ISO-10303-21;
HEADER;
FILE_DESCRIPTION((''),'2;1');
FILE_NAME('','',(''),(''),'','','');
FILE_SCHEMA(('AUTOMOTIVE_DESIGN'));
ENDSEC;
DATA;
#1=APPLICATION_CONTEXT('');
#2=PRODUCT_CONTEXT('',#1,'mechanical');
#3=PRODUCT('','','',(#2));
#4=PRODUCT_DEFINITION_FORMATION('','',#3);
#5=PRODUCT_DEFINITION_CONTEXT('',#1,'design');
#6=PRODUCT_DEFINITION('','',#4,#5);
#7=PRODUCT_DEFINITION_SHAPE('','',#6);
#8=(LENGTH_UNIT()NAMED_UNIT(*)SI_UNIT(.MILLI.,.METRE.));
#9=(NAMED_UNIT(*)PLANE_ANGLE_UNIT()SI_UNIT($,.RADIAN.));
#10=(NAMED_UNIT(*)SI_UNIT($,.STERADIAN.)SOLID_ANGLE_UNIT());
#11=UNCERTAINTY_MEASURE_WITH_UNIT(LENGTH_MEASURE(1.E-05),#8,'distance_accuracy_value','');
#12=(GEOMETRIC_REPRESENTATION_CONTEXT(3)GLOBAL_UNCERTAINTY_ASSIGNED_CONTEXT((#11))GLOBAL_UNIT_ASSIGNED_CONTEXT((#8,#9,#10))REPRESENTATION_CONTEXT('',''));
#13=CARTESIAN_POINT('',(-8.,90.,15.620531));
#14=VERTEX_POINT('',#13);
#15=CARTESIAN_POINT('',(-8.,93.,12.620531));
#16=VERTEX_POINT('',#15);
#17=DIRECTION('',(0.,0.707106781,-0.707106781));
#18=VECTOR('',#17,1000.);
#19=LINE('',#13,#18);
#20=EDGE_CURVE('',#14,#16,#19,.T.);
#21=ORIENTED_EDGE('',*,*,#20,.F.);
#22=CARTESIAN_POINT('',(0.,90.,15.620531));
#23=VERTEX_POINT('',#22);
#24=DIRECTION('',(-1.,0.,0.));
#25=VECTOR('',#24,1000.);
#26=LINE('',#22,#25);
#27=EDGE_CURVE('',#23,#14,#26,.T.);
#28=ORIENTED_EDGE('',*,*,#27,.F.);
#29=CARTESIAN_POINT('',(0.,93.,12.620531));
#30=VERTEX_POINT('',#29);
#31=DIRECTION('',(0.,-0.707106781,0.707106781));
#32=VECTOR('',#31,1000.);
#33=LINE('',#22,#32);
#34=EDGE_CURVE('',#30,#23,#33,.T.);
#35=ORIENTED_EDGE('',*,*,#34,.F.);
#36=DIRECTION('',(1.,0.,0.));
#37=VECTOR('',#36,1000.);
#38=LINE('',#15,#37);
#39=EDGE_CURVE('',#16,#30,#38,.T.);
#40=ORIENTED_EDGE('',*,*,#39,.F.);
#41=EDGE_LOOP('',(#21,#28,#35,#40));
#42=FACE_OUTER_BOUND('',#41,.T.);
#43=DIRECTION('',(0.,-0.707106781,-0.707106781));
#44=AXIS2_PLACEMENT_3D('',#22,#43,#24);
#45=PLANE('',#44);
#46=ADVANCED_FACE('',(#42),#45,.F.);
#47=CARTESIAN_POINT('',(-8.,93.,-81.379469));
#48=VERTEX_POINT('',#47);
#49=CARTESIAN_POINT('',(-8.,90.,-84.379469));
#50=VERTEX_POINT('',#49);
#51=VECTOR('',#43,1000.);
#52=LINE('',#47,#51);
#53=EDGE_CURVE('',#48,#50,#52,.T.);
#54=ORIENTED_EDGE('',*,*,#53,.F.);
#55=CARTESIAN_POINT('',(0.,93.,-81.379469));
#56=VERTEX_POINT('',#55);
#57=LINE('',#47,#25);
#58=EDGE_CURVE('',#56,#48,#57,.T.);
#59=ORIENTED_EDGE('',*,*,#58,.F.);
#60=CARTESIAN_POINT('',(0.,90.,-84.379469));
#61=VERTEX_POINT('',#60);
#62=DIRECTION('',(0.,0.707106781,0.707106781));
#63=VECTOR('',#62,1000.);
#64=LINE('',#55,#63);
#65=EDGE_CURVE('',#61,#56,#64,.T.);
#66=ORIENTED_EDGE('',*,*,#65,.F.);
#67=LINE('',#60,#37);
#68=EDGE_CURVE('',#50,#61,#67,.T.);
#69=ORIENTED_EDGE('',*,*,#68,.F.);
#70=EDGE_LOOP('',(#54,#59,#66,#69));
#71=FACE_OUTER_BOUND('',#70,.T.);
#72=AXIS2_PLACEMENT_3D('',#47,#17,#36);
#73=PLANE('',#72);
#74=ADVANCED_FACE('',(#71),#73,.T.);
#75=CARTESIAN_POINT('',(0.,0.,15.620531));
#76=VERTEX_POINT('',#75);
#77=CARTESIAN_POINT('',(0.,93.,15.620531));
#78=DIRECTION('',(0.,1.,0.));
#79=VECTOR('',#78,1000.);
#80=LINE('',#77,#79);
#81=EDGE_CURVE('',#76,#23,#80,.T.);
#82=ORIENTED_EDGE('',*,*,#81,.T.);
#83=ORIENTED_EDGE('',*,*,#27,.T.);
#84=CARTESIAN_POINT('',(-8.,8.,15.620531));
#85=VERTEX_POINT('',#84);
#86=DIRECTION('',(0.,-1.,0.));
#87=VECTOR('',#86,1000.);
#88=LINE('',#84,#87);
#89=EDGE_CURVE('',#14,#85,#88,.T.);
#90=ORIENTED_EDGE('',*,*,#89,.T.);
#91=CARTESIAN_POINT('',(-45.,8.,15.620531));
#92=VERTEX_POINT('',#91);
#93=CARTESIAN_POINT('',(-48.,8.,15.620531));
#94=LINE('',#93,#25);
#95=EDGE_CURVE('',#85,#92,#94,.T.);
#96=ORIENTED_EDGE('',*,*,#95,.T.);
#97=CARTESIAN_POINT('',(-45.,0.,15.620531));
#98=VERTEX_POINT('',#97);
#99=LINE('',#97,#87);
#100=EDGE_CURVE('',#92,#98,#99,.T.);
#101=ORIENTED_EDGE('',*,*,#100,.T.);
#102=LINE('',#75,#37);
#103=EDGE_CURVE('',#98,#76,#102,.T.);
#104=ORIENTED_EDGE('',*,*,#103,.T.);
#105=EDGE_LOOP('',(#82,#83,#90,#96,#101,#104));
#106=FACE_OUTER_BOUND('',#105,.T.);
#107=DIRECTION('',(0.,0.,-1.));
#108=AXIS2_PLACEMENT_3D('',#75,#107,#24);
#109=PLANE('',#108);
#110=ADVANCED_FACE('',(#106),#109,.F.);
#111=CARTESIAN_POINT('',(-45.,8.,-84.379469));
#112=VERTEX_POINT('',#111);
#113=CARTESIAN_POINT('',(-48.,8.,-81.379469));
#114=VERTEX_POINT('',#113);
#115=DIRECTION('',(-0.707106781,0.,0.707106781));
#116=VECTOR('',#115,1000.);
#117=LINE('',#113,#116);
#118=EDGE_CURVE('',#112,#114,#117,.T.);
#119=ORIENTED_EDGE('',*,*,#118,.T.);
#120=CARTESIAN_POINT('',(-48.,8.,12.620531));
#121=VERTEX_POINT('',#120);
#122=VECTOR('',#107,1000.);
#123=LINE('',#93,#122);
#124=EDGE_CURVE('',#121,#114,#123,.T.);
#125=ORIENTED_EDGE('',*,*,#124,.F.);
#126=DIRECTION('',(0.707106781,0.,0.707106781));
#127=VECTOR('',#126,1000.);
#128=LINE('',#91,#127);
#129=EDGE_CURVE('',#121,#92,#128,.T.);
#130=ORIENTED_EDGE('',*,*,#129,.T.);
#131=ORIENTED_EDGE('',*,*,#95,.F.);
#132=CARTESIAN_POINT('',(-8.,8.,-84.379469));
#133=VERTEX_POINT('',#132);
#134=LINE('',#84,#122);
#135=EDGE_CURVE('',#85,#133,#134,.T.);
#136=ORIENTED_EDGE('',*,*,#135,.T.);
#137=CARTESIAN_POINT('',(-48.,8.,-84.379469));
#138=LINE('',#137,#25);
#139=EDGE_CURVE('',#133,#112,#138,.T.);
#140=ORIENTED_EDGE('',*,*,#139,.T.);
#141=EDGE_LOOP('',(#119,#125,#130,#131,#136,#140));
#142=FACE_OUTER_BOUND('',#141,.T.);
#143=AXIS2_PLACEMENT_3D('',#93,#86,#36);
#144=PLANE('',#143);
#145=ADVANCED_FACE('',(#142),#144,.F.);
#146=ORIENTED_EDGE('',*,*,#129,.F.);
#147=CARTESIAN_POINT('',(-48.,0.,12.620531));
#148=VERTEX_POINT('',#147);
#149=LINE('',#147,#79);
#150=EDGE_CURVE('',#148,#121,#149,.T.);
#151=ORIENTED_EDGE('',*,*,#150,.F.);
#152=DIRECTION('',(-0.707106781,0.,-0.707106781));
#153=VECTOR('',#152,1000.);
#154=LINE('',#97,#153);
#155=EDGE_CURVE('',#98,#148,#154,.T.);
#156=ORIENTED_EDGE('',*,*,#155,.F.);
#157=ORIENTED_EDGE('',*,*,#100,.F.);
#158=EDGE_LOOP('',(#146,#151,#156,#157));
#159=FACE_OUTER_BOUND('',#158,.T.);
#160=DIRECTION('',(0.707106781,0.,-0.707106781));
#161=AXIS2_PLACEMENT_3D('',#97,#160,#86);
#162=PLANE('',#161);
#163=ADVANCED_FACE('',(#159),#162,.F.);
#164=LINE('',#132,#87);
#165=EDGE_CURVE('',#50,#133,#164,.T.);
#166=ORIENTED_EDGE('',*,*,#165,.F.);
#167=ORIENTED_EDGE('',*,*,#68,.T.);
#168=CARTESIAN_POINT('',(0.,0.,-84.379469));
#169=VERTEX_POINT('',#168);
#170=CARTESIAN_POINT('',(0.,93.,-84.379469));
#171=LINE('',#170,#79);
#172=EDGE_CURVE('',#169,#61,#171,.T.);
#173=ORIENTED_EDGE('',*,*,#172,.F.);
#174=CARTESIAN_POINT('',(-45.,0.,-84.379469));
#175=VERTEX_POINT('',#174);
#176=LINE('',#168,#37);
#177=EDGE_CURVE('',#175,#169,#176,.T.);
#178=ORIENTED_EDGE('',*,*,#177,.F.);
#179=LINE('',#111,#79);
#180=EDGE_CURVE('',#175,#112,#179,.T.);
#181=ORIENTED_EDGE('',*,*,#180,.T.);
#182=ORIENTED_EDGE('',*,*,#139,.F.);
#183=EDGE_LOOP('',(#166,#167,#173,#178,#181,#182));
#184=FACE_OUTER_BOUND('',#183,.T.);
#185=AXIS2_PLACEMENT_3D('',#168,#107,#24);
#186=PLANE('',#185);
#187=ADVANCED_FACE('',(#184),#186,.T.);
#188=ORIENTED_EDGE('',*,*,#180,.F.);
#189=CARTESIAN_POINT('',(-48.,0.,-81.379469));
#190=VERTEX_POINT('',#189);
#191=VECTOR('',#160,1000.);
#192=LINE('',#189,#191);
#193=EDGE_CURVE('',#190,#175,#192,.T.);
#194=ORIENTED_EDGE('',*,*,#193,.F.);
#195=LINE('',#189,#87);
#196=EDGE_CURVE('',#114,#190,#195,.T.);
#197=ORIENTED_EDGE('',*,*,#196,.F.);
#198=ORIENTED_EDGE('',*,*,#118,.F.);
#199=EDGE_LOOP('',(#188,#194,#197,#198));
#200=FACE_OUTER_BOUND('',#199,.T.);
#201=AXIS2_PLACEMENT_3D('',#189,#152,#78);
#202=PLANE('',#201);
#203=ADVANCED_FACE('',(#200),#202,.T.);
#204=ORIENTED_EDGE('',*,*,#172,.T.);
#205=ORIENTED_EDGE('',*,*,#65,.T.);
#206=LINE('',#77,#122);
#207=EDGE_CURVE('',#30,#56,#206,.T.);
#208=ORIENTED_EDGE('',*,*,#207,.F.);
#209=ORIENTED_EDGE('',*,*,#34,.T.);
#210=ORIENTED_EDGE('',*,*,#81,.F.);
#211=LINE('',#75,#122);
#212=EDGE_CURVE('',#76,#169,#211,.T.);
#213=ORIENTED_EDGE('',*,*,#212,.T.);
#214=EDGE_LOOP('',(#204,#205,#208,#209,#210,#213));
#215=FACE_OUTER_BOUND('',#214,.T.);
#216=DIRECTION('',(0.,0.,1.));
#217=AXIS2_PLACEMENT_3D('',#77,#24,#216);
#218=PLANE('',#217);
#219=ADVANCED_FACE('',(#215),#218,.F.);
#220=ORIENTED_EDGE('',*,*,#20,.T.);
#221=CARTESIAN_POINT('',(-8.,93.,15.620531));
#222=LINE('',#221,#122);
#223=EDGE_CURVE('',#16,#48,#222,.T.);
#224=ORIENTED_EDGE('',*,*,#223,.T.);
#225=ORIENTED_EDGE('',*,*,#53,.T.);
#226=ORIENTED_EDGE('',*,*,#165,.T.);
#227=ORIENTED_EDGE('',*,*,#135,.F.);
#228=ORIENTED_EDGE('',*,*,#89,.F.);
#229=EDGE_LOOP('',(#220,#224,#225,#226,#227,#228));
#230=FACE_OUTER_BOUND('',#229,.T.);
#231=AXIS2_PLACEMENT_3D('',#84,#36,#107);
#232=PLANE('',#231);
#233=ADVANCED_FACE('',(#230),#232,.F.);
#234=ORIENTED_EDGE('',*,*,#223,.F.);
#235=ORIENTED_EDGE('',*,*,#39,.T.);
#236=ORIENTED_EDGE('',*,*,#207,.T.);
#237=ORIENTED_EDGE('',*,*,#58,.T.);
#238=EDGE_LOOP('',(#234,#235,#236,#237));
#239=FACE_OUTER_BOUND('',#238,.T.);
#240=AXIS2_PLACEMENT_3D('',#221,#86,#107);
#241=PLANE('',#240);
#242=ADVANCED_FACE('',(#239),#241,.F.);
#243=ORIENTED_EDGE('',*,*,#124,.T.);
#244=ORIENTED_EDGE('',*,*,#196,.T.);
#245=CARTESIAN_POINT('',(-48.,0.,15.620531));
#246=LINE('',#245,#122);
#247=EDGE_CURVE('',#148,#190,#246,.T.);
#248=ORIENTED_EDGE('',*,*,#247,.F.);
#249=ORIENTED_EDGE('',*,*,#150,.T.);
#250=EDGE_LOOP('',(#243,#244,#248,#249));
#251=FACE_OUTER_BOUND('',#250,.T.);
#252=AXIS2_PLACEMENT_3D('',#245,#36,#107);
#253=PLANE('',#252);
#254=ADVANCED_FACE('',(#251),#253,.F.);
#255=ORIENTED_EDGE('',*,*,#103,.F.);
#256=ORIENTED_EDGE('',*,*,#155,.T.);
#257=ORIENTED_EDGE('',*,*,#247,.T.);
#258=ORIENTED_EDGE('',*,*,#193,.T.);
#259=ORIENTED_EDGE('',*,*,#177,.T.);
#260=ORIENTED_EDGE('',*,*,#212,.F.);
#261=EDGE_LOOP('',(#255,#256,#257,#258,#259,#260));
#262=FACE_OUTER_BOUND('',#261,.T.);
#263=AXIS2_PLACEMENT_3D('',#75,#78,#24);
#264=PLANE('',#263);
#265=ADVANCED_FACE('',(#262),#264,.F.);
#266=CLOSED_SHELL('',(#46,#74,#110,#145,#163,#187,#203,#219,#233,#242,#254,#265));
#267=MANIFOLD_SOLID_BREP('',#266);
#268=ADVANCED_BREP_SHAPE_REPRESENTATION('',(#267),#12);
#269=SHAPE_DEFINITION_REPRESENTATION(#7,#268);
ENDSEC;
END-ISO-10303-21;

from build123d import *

# Parameters (mm, degrees)
EXTRUDE_1_DEPTH = 50
CHAMFER_1_SIZE  = 3


with BuildPart() as part:
    # 草图2 → 凸台-拉伸1 (new, symmetric)
    with BuildSketch(Plane(origin=(409.637600706, 0.5, -34.379468655), x_dir=(1, 0, 0), z_dir=(0, 0, 1))):
        Polygon((-409.637600706, 92.5), (-409.637600706, -0.5), (-457.637600706, -0.5), (-457.637600706, 7.5), (-417.637600706, 7.5), (-417.637600706, 92.5), align=None)
    extrude(amount=EXTRUDE_1_DEPTH, both=True)

    # 倒角1
    chamfer_1_edges = [part.edges().sort_by_distance(p)[0] for p in [
        (-48, 4, 15.620531345),
        (-4, 93, 15.620531345),
        (-48, 4, -84.379468655),
        (-4, 93, -84.379468655),
    ]]
    chamfer(chamfer_1_edges, length=CHAMFER_1_SIZE)


solid = part.part
